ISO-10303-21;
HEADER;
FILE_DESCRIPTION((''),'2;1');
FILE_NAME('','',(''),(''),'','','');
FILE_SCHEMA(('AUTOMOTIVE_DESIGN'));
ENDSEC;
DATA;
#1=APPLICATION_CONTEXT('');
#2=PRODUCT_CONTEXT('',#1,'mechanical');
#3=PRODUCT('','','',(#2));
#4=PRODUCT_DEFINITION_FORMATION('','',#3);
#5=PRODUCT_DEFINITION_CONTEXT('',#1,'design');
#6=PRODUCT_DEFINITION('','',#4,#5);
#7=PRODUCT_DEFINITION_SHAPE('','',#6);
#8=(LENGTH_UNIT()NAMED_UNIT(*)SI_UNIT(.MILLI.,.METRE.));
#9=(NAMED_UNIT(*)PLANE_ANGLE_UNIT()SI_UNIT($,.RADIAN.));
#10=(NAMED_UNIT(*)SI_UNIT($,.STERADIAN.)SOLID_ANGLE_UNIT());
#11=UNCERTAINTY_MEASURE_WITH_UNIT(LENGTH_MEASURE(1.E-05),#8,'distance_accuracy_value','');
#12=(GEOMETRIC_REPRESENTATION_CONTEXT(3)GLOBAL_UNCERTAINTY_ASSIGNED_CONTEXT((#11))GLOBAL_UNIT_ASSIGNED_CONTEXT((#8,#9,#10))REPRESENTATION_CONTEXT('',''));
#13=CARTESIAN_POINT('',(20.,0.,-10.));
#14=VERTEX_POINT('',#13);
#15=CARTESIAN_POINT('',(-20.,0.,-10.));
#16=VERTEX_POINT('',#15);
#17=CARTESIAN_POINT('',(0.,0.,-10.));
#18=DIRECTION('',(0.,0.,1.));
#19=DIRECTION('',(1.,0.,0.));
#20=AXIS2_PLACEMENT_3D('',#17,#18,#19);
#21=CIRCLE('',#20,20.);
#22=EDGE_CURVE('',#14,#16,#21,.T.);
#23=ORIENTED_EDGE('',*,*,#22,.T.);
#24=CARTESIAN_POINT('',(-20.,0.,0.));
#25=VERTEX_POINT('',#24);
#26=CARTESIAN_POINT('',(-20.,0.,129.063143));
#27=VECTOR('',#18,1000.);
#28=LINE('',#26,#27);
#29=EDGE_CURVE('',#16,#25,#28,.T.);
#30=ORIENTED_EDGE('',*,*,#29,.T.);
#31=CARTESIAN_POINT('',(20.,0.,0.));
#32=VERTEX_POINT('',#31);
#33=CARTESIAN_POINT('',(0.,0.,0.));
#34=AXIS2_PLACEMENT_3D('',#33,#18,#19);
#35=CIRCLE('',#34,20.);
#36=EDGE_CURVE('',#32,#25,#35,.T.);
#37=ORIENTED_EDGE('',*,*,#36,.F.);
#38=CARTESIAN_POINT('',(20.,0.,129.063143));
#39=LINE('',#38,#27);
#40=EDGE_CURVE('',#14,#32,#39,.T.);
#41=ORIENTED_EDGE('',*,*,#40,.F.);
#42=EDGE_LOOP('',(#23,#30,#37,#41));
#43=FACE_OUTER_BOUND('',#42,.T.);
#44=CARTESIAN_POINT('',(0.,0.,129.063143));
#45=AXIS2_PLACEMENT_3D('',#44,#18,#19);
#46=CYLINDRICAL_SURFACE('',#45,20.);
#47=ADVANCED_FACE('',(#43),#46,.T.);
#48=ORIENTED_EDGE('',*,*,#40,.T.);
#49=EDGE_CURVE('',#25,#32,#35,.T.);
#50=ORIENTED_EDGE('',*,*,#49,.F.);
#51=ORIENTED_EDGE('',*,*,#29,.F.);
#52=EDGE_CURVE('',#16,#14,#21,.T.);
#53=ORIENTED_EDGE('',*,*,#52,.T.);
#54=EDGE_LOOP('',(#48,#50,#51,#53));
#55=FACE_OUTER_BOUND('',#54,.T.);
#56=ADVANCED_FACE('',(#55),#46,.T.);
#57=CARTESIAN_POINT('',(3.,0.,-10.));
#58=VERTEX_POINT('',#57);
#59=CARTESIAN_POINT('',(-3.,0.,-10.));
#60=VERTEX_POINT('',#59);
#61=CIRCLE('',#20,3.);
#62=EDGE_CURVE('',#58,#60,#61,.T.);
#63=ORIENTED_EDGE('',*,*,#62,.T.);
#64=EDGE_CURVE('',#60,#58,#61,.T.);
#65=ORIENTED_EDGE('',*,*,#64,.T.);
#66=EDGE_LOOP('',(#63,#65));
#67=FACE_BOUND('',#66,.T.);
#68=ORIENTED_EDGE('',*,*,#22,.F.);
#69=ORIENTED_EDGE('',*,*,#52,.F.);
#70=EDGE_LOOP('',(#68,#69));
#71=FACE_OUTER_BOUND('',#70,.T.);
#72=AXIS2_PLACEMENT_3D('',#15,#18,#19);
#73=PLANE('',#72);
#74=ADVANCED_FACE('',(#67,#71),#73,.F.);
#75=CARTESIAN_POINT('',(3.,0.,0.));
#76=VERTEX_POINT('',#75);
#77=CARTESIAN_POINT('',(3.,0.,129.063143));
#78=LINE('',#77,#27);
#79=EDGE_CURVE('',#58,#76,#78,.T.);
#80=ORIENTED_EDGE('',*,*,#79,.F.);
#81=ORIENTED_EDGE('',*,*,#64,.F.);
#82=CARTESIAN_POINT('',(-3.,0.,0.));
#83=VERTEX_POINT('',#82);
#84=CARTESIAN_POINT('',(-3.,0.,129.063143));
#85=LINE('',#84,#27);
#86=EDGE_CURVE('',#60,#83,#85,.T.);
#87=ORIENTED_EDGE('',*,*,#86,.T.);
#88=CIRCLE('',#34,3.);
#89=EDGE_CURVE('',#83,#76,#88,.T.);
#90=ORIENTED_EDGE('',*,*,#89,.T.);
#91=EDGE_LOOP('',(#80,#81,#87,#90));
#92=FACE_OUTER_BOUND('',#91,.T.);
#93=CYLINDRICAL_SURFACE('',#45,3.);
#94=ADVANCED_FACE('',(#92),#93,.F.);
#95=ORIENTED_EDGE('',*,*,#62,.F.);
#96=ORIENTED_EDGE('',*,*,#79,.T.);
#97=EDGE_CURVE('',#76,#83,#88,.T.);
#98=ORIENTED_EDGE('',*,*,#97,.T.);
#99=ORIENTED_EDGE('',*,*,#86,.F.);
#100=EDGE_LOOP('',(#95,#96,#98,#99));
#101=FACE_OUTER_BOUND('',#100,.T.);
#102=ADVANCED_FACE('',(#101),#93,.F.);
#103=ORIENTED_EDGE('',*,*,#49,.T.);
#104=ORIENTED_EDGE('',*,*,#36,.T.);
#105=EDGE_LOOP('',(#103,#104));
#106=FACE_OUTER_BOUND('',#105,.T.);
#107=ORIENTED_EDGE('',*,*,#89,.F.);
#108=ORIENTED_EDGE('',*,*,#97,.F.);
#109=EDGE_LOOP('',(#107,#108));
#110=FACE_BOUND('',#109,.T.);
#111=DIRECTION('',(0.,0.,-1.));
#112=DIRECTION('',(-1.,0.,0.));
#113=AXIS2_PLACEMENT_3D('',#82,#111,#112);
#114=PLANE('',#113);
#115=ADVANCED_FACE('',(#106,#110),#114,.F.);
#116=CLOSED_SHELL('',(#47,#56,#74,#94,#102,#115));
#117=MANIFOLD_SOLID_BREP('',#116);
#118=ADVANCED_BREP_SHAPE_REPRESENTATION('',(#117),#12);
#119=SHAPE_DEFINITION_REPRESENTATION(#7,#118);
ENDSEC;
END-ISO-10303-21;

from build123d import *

# Parameters (mm, degrees)
SKETCH_1_W = 17
SKETCH_1_H = 10


with BuildPart() as part:
    # 草图1 → 旋转1 (revolve)
    with BuildSketch(Plane(origin=(0, 0, 0), x_dir=(1, 0, 0), z_dir=(0, 1, 0)), mode=Mode.PRIVATE) as revolve_1_sk:
        with Locations((-11.5, 5)):
            Rectangle(SKETCH_1_W, SKETCH_1_H)
    revolve(revolve_1_sk.sketch.rotate(Axis((0, 0, 129.063142874), (0, 0, -1)), 180), axis=Axis((0, 0, 129.063142874), (0, 0, -1)))


solid = part.part
